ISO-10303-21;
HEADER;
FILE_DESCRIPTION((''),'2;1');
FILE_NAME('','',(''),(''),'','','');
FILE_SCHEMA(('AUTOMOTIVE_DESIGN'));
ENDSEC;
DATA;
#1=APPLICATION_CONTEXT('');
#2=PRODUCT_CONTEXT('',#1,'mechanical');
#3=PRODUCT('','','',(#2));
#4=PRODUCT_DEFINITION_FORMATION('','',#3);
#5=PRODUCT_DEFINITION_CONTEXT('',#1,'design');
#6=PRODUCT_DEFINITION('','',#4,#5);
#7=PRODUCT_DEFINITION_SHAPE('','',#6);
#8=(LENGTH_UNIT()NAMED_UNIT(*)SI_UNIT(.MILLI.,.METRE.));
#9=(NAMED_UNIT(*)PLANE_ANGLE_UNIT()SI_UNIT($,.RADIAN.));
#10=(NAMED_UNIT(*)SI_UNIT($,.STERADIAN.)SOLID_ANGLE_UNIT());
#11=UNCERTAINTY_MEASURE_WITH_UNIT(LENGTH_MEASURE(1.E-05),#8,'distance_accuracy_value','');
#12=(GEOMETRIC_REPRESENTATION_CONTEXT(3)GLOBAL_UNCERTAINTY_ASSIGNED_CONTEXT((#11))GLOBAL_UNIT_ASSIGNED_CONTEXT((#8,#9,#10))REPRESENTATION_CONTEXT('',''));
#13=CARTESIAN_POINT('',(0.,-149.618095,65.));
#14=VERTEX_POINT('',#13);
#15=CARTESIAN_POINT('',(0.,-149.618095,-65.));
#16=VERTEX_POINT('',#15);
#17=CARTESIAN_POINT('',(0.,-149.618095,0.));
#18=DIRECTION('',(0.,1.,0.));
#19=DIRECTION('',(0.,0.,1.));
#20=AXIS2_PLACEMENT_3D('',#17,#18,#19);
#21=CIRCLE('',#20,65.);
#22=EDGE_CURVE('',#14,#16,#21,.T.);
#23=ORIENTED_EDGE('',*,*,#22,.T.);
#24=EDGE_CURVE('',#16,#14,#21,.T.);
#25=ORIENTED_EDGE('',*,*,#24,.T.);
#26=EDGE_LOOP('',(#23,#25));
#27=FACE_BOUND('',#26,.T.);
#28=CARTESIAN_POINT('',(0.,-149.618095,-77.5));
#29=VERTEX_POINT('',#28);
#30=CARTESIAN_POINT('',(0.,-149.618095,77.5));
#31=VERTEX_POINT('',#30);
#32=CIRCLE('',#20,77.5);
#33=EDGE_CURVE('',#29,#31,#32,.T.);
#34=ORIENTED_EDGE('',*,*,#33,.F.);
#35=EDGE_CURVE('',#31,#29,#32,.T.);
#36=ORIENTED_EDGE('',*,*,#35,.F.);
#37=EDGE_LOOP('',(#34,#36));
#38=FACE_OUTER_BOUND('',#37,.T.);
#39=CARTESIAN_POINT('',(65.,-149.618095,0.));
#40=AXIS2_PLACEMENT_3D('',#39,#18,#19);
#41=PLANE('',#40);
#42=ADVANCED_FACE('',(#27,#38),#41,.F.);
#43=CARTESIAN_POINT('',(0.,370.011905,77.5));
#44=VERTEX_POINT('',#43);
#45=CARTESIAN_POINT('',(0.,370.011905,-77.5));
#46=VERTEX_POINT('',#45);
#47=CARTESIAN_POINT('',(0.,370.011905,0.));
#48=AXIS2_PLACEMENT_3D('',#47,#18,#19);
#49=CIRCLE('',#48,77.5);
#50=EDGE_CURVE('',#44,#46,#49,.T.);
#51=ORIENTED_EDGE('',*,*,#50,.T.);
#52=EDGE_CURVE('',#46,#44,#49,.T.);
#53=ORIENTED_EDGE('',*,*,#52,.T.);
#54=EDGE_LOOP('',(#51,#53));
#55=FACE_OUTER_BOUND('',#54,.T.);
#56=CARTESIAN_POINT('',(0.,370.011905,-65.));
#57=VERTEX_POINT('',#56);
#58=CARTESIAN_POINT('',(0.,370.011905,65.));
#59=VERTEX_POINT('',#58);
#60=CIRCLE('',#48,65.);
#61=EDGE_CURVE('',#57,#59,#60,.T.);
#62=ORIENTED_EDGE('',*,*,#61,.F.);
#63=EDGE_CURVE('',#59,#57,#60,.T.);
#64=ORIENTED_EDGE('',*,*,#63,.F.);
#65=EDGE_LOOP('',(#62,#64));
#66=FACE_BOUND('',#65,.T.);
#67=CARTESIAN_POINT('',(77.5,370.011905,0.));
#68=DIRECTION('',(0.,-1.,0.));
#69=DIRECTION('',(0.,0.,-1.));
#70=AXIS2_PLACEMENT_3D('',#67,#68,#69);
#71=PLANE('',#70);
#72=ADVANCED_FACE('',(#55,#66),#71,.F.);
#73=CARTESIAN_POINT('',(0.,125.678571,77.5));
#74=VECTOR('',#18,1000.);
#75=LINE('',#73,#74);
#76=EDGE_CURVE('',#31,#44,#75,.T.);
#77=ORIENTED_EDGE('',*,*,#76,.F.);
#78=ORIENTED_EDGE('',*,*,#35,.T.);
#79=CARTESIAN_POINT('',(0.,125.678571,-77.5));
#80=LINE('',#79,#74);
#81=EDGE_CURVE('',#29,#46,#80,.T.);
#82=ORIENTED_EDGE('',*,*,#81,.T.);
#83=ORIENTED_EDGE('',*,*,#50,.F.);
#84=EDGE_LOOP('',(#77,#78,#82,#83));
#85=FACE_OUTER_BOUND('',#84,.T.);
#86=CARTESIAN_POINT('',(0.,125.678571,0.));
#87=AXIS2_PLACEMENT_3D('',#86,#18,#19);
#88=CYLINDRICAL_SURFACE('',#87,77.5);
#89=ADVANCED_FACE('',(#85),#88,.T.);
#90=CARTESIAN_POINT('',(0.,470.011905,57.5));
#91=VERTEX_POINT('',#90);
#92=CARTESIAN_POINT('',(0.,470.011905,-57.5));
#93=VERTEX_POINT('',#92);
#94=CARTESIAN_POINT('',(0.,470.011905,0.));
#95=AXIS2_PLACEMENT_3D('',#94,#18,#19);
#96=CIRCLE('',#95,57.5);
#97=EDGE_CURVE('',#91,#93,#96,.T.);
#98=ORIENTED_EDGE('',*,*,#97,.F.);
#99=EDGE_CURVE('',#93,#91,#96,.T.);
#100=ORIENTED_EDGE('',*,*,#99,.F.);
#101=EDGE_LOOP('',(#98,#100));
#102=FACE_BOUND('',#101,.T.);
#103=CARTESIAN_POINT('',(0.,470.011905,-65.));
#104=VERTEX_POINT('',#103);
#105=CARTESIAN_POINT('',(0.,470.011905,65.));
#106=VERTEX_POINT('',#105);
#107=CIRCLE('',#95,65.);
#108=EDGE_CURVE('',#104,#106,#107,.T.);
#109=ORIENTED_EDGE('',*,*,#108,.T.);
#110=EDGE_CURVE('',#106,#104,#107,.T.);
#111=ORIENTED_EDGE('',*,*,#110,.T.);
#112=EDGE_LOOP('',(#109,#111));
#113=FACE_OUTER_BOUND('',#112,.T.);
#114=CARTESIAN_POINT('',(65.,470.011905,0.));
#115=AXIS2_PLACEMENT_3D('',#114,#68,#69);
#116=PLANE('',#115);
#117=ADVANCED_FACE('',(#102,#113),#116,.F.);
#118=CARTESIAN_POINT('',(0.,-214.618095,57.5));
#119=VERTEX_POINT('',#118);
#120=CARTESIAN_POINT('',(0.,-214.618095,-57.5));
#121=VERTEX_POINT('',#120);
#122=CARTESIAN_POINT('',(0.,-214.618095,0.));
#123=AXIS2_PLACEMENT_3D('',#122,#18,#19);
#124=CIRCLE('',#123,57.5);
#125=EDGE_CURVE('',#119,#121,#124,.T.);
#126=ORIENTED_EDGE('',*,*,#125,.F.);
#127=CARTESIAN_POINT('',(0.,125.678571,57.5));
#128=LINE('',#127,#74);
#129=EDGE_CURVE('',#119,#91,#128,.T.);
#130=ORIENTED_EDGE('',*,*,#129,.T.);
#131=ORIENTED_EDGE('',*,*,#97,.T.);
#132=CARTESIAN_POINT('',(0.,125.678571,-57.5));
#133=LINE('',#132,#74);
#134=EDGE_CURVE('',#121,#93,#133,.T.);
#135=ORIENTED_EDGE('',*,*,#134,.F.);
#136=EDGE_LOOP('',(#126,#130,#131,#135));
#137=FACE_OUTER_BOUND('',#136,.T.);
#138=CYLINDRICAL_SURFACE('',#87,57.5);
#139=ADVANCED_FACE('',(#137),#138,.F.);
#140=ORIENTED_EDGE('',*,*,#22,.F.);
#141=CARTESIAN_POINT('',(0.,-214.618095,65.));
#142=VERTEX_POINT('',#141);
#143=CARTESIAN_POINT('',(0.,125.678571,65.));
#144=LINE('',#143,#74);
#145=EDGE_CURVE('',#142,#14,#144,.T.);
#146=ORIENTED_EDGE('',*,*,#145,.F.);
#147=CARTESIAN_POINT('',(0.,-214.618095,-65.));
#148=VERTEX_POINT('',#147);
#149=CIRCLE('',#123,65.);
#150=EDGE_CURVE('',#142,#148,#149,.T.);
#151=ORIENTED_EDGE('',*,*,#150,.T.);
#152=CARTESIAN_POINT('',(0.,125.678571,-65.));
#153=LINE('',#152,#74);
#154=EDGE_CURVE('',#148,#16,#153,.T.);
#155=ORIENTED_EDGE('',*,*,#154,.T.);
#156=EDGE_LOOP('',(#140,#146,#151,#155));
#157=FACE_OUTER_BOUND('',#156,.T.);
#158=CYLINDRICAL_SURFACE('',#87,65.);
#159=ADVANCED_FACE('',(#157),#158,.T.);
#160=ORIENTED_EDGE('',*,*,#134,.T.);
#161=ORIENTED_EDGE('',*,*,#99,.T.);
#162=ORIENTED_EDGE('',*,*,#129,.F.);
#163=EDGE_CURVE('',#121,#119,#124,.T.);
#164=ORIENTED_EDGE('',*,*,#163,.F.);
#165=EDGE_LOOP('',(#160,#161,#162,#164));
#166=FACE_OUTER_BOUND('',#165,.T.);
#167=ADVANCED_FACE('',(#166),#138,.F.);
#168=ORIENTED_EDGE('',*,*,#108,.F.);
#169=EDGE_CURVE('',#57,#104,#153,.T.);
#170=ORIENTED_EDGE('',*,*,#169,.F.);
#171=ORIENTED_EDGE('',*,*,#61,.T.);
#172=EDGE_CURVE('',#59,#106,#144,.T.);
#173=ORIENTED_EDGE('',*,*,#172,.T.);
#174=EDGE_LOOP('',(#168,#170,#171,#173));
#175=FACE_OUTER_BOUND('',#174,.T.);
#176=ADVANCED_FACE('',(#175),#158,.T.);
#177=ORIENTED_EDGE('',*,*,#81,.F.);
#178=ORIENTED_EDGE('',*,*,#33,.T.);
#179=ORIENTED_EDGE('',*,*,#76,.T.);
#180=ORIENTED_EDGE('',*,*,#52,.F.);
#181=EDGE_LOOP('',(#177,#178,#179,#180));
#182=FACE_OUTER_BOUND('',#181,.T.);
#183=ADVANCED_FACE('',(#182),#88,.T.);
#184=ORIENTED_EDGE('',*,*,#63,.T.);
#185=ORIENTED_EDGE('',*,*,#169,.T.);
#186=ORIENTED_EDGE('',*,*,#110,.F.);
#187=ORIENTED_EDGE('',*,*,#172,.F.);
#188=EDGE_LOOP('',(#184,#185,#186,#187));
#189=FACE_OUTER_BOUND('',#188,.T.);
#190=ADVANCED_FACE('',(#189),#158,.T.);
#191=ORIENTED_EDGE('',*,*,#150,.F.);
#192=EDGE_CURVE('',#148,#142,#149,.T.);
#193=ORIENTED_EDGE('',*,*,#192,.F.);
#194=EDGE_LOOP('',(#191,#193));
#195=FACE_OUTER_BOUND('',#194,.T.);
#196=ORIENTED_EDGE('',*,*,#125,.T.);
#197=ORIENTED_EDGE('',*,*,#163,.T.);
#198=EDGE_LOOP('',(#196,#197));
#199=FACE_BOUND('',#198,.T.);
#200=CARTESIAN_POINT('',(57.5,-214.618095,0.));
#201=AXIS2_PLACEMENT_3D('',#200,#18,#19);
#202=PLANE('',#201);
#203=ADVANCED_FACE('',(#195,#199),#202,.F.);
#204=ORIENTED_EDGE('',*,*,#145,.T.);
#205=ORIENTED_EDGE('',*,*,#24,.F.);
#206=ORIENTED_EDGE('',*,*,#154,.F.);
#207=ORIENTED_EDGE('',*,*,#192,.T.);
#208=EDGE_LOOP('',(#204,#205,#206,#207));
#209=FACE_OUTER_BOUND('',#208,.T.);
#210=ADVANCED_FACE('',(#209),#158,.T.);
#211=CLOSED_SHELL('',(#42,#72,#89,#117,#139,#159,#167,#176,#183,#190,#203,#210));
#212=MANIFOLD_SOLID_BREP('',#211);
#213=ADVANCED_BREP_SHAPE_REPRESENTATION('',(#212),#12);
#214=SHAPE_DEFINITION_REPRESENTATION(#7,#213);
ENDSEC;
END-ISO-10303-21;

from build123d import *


with BuildPart() as part:
    # 草图1 → 旋转1 (revolve)
    with BuildSketch(Plane.XY, mode=Mode.PRIVATE) as revolve_1_sk:
        Polygon((57.5, 470.011904762), (57.5, -214.618095238), (65, -214.618095238), (65, -149.618095238), (77.5, -149.618095238), (77.5, 370.011904762), (65, 370.011904762), (65, 470.011904762), align=None)
    revolve(revolve_1_sk.sketch.rotate(Axis((0, 125.678571429, 0), (0, -1, 0)), 90), axis=Axis((0, 125.678571429, 0), (0, -1, 0)))


solid = part.part
